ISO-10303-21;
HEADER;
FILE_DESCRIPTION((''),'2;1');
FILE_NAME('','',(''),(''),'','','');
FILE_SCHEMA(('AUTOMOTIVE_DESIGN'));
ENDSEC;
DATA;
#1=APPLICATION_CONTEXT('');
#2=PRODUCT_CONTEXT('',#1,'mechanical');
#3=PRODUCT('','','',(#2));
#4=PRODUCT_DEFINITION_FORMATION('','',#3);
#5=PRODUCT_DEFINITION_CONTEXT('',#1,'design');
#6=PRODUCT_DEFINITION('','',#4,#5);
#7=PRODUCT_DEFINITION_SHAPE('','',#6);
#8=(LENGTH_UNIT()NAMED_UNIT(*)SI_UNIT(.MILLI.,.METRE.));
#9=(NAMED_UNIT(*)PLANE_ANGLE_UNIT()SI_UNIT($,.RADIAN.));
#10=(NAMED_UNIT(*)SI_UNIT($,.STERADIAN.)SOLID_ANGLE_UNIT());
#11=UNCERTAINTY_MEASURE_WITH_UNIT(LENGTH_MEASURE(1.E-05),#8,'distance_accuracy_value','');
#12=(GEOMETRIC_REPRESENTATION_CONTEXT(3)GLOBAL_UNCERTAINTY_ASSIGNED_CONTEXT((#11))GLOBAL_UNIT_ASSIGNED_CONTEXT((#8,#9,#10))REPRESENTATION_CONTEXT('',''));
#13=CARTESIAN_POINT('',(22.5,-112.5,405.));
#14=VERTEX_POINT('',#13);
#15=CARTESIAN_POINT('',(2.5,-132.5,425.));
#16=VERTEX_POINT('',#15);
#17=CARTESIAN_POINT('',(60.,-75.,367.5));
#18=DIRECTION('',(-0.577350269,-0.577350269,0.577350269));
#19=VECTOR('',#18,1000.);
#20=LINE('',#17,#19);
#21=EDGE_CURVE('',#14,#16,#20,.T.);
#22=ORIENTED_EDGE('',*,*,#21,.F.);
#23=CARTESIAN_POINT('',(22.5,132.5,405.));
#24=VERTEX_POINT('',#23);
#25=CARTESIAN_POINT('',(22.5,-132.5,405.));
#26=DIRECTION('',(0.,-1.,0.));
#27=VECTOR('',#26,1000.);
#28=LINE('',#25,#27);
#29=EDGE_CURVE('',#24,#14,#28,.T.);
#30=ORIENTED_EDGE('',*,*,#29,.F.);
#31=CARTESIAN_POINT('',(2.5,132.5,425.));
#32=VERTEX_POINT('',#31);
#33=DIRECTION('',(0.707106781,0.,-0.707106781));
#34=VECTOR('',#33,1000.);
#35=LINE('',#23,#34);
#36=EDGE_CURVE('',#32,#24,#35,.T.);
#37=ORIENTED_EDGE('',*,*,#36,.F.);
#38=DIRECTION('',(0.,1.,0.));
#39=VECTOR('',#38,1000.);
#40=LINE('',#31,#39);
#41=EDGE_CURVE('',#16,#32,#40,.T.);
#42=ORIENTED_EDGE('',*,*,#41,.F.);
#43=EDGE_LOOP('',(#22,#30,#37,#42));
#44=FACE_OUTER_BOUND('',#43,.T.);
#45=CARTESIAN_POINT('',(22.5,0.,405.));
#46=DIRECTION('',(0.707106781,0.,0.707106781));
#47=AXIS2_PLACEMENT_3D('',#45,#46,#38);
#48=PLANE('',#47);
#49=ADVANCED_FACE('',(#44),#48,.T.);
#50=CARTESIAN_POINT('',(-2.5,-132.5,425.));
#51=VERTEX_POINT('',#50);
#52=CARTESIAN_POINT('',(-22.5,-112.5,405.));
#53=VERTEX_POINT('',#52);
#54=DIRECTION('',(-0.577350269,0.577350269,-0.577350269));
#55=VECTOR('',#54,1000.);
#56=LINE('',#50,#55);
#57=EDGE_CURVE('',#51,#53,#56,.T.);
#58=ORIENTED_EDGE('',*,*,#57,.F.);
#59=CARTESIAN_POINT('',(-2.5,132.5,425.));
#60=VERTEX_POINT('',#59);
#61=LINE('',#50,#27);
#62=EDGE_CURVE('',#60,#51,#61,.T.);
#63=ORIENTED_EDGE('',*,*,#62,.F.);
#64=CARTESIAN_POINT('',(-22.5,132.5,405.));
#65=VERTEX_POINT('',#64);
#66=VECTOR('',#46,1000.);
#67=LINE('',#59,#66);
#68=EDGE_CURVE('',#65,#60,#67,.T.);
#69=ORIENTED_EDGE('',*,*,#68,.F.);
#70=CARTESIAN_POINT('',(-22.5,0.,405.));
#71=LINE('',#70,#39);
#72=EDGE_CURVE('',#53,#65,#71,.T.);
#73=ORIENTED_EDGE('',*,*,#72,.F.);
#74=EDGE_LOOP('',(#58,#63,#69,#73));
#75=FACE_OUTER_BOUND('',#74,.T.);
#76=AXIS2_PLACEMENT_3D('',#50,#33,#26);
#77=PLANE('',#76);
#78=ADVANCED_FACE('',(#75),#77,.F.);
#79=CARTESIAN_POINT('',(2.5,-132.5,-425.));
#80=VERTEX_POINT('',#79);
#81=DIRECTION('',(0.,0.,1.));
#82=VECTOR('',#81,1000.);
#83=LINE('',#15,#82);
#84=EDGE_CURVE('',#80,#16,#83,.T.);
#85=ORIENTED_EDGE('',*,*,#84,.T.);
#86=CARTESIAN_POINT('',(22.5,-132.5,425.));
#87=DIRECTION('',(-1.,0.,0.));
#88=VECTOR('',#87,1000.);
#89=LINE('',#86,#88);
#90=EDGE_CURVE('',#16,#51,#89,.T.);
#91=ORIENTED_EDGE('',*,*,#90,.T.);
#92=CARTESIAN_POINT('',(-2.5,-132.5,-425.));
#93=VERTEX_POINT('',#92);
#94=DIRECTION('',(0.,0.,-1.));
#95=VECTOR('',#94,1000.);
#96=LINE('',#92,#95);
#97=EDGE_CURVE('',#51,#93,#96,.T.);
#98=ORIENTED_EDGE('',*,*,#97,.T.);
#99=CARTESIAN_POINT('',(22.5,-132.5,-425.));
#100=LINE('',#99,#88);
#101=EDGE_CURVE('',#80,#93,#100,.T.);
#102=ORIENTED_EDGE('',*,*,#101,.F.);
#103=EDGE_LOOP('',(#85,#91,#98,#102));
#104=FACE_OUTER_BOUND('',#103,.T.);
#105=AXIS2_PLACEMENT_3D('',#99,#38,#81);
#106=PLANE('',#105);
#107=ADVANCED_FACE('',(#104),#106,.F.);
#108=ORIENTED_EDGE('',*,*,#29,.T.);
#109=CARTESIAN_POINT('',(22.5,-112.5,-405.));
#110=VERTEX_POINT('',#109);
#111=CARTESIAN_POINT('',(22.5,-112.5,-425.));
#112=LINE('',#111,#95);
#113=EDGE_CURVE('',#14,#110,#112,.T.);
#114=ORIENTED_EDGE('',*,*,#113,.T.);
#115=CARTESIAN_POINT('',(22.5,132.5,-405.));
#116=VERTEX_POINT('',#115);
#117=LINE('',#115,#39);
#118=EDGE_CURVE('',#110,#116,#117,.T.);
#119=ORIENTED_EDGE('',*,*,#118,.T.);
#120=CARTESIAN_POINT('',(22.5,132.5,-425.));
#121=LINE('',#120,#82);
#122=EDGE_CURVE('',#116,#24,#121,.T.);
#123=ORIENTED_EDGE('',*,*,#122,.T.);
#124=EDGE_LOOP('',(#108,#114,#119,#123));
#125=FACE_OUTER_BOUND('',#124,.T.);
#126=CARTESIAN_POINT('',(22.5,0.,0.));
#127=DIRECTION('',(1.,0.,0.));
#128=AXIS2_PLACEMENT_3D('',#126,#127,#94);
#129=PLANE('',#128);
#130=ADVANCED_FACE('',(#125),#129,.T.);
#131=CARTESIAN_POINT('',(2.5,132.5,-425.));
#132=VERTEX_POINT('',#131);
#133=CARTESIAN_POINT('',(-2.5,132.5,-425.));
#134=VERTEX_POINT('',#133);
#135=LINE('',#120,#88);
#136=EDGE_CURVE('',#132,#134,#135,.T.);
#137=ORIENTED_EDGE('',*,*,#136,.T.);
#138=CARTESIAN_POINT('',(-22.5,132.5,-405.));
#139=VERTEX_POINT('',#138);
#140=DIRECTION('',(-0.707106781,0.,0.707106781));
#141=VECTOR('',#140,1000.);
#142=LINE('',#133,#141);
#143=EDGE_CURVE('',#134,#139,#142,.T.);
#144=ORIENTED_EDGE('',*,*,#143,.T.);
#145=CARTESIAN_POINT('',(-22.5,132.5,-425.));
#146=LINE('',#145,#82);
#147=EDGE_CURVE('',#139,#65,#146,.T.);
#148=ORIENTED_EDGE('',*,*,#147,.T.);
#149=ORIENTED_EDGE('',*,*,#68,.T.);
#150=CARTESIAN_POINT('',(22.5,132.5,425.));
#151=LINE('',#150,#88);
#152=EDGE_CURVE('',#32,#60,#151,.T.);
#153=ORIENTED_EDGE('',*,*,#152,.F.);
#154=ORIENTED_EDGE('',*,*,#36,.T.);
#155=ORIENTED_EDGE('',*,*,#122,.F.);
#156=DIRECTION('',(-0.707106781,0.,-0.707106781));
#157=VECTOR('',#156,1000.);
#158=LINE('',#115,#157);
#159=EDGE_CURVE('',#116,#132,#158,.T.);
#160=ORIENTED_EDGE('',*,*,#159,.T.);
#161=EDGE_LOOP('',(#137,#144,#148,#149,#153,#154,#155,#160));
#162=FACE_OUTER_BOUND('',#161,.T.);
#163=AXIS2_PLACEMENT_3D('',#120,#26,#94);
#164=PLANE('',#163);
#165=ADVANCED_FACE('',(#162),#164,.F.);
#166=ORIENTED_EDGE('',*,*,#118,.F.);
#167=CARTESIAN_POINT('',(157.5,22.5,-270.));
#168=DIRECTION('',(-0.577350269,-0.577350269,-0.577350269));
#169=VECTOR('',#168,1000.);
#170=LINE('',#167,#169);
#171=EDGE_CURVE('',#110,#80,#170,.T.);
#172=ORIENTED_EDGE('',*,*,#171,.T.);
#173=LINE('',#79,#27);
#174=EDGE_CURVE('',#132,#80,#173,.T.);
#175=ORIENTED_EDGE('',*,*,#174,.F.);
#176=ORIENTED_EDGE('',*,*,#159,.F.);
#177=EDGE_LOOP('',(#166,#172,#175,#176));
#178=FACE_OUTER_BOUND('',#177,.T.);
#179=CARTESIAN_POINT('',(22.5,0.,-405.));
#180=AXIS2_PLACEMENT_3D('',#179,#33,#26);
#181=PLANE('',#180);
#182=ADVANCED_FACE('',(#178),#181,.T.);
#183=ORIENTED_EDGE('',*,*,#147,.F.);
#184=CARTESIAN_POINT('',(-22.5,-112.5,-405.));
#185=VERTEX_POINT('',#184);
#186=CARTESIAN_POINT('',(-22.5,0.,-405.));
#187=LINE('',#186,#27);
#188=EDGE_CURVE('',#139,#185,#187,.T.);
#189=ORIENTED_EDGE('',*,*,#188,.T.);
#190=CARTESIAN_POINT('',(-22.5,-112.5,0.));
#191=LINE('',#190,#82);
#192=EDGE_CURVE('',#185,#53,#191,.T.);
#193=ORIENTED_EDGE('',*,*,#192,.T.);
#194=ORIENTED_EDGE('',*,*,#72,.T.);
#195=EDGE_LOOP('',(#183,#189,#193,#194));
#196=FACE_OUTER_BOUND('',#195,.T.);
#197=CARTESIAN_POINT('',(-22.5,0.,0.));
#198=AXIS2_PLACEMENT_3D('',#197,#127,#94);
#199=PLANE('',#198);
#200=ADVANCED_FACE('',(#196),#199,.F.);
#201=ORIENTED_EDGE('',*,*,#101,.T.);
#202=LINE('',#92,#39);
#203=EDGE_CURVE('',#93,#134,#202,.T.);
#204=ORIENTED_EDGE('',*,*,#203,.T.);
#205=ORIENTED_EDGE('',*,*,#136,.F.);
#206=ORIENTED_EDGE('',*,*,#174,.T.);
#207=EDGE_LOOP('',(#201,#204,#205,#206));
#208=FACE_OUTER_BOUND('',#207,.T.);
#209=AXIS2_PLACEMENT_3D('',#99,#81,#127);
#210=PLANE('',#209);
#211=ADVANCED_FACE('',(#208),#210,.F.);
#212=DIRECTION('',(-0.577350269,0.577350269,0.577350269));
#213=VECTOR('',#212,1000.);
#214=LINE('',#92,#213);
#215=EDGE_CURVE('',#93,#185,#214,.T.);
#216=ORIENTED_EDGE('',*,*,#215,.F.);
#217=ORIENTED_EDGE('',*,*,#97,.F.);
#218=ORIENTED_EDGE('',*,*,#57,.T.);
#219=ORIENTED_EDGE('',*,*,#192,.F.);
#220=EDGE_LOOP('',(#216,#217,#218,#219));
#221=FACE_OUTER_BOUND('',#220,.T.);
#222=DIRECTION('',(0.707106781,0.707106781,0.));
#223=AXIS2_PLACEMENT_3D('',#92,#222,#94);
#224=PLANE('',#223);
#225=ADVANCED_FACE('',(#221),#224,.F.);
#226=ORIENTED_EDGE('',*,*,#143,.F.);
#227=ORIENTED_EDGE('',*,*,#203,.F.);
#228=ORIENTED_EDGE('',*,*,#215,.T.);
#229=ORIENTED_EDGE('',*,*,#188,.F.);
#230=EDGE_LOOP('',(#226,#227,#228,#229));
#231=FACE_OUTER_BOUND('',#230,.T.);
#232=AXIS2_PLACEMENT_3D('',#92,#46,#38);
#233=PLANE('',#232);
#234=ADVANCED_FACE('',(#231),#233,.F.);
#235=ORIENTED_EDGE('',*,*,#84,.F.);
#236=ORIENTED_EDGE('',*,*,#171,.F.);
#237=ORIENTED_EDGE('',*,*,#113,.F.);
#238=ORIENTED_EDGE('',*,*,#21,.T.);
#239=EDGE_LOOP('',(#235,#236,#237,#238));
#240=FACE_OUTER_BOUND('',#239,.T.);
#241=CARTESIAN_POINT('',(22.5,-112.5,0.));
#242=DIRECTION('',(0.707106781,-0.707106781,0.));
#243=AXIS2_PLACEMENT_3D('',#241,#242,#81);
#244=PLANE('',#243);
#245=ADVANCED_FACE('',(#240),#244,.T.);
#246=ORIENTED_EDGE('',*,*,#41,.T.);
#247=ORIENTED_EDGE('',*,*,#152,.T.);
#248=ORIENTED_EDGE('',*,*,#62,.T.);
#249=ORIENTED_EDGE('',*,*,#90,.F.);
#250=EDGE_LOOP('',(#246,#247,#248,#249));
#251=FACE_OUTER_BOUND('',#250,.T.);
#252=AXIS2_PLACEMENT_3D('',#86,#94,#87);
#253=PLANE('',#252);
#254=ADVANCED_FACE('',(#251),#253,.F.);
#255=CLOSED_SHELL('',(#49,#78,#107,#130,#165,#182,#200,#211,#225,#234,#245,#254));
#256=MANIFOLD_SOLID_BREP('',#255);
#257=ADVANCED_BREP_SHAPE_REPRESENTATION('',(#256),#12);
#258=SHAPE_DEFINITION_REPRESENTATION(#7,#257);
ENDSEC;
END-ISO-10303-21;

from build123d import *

# Parameters (mm, degrees)
SKETCH1_W           = 850
SKETCH1_H           = 265
BOSS_EXTRUDE1_DEPTH = 22.5
CHAMFER1_SIZE       = 20


with BuildPart() as part:
    # Sketch1 → Boss-Extrude1 (new, symmetric)
    with BuildSketch(Plane(origin=(0, 0, 0), x_dir=(0, 0, -1), z_dir=(1, 0, 0))):
        Rectangle(SKETCH1_W, SKETCH1_H)
    extrude(amount=BOSS_EXTRUDE1_DEPTH, both=True)

    # Chamfer1
    chamfer1_edges = [part.edges().sort_by_distance(p)[0] for p in [
        (22.5, 0, -425),
        (22.5, 0, 425),
        (-22.5, 0, -425),
        (-22.5, -132.5, 0),
        (-22.5, 0, 425),
        (22.5, -132.5, 0),
    ]]
    chamfer(chamfer1_edges, length=CHAMFER1_SIZE)


solid = part.part
